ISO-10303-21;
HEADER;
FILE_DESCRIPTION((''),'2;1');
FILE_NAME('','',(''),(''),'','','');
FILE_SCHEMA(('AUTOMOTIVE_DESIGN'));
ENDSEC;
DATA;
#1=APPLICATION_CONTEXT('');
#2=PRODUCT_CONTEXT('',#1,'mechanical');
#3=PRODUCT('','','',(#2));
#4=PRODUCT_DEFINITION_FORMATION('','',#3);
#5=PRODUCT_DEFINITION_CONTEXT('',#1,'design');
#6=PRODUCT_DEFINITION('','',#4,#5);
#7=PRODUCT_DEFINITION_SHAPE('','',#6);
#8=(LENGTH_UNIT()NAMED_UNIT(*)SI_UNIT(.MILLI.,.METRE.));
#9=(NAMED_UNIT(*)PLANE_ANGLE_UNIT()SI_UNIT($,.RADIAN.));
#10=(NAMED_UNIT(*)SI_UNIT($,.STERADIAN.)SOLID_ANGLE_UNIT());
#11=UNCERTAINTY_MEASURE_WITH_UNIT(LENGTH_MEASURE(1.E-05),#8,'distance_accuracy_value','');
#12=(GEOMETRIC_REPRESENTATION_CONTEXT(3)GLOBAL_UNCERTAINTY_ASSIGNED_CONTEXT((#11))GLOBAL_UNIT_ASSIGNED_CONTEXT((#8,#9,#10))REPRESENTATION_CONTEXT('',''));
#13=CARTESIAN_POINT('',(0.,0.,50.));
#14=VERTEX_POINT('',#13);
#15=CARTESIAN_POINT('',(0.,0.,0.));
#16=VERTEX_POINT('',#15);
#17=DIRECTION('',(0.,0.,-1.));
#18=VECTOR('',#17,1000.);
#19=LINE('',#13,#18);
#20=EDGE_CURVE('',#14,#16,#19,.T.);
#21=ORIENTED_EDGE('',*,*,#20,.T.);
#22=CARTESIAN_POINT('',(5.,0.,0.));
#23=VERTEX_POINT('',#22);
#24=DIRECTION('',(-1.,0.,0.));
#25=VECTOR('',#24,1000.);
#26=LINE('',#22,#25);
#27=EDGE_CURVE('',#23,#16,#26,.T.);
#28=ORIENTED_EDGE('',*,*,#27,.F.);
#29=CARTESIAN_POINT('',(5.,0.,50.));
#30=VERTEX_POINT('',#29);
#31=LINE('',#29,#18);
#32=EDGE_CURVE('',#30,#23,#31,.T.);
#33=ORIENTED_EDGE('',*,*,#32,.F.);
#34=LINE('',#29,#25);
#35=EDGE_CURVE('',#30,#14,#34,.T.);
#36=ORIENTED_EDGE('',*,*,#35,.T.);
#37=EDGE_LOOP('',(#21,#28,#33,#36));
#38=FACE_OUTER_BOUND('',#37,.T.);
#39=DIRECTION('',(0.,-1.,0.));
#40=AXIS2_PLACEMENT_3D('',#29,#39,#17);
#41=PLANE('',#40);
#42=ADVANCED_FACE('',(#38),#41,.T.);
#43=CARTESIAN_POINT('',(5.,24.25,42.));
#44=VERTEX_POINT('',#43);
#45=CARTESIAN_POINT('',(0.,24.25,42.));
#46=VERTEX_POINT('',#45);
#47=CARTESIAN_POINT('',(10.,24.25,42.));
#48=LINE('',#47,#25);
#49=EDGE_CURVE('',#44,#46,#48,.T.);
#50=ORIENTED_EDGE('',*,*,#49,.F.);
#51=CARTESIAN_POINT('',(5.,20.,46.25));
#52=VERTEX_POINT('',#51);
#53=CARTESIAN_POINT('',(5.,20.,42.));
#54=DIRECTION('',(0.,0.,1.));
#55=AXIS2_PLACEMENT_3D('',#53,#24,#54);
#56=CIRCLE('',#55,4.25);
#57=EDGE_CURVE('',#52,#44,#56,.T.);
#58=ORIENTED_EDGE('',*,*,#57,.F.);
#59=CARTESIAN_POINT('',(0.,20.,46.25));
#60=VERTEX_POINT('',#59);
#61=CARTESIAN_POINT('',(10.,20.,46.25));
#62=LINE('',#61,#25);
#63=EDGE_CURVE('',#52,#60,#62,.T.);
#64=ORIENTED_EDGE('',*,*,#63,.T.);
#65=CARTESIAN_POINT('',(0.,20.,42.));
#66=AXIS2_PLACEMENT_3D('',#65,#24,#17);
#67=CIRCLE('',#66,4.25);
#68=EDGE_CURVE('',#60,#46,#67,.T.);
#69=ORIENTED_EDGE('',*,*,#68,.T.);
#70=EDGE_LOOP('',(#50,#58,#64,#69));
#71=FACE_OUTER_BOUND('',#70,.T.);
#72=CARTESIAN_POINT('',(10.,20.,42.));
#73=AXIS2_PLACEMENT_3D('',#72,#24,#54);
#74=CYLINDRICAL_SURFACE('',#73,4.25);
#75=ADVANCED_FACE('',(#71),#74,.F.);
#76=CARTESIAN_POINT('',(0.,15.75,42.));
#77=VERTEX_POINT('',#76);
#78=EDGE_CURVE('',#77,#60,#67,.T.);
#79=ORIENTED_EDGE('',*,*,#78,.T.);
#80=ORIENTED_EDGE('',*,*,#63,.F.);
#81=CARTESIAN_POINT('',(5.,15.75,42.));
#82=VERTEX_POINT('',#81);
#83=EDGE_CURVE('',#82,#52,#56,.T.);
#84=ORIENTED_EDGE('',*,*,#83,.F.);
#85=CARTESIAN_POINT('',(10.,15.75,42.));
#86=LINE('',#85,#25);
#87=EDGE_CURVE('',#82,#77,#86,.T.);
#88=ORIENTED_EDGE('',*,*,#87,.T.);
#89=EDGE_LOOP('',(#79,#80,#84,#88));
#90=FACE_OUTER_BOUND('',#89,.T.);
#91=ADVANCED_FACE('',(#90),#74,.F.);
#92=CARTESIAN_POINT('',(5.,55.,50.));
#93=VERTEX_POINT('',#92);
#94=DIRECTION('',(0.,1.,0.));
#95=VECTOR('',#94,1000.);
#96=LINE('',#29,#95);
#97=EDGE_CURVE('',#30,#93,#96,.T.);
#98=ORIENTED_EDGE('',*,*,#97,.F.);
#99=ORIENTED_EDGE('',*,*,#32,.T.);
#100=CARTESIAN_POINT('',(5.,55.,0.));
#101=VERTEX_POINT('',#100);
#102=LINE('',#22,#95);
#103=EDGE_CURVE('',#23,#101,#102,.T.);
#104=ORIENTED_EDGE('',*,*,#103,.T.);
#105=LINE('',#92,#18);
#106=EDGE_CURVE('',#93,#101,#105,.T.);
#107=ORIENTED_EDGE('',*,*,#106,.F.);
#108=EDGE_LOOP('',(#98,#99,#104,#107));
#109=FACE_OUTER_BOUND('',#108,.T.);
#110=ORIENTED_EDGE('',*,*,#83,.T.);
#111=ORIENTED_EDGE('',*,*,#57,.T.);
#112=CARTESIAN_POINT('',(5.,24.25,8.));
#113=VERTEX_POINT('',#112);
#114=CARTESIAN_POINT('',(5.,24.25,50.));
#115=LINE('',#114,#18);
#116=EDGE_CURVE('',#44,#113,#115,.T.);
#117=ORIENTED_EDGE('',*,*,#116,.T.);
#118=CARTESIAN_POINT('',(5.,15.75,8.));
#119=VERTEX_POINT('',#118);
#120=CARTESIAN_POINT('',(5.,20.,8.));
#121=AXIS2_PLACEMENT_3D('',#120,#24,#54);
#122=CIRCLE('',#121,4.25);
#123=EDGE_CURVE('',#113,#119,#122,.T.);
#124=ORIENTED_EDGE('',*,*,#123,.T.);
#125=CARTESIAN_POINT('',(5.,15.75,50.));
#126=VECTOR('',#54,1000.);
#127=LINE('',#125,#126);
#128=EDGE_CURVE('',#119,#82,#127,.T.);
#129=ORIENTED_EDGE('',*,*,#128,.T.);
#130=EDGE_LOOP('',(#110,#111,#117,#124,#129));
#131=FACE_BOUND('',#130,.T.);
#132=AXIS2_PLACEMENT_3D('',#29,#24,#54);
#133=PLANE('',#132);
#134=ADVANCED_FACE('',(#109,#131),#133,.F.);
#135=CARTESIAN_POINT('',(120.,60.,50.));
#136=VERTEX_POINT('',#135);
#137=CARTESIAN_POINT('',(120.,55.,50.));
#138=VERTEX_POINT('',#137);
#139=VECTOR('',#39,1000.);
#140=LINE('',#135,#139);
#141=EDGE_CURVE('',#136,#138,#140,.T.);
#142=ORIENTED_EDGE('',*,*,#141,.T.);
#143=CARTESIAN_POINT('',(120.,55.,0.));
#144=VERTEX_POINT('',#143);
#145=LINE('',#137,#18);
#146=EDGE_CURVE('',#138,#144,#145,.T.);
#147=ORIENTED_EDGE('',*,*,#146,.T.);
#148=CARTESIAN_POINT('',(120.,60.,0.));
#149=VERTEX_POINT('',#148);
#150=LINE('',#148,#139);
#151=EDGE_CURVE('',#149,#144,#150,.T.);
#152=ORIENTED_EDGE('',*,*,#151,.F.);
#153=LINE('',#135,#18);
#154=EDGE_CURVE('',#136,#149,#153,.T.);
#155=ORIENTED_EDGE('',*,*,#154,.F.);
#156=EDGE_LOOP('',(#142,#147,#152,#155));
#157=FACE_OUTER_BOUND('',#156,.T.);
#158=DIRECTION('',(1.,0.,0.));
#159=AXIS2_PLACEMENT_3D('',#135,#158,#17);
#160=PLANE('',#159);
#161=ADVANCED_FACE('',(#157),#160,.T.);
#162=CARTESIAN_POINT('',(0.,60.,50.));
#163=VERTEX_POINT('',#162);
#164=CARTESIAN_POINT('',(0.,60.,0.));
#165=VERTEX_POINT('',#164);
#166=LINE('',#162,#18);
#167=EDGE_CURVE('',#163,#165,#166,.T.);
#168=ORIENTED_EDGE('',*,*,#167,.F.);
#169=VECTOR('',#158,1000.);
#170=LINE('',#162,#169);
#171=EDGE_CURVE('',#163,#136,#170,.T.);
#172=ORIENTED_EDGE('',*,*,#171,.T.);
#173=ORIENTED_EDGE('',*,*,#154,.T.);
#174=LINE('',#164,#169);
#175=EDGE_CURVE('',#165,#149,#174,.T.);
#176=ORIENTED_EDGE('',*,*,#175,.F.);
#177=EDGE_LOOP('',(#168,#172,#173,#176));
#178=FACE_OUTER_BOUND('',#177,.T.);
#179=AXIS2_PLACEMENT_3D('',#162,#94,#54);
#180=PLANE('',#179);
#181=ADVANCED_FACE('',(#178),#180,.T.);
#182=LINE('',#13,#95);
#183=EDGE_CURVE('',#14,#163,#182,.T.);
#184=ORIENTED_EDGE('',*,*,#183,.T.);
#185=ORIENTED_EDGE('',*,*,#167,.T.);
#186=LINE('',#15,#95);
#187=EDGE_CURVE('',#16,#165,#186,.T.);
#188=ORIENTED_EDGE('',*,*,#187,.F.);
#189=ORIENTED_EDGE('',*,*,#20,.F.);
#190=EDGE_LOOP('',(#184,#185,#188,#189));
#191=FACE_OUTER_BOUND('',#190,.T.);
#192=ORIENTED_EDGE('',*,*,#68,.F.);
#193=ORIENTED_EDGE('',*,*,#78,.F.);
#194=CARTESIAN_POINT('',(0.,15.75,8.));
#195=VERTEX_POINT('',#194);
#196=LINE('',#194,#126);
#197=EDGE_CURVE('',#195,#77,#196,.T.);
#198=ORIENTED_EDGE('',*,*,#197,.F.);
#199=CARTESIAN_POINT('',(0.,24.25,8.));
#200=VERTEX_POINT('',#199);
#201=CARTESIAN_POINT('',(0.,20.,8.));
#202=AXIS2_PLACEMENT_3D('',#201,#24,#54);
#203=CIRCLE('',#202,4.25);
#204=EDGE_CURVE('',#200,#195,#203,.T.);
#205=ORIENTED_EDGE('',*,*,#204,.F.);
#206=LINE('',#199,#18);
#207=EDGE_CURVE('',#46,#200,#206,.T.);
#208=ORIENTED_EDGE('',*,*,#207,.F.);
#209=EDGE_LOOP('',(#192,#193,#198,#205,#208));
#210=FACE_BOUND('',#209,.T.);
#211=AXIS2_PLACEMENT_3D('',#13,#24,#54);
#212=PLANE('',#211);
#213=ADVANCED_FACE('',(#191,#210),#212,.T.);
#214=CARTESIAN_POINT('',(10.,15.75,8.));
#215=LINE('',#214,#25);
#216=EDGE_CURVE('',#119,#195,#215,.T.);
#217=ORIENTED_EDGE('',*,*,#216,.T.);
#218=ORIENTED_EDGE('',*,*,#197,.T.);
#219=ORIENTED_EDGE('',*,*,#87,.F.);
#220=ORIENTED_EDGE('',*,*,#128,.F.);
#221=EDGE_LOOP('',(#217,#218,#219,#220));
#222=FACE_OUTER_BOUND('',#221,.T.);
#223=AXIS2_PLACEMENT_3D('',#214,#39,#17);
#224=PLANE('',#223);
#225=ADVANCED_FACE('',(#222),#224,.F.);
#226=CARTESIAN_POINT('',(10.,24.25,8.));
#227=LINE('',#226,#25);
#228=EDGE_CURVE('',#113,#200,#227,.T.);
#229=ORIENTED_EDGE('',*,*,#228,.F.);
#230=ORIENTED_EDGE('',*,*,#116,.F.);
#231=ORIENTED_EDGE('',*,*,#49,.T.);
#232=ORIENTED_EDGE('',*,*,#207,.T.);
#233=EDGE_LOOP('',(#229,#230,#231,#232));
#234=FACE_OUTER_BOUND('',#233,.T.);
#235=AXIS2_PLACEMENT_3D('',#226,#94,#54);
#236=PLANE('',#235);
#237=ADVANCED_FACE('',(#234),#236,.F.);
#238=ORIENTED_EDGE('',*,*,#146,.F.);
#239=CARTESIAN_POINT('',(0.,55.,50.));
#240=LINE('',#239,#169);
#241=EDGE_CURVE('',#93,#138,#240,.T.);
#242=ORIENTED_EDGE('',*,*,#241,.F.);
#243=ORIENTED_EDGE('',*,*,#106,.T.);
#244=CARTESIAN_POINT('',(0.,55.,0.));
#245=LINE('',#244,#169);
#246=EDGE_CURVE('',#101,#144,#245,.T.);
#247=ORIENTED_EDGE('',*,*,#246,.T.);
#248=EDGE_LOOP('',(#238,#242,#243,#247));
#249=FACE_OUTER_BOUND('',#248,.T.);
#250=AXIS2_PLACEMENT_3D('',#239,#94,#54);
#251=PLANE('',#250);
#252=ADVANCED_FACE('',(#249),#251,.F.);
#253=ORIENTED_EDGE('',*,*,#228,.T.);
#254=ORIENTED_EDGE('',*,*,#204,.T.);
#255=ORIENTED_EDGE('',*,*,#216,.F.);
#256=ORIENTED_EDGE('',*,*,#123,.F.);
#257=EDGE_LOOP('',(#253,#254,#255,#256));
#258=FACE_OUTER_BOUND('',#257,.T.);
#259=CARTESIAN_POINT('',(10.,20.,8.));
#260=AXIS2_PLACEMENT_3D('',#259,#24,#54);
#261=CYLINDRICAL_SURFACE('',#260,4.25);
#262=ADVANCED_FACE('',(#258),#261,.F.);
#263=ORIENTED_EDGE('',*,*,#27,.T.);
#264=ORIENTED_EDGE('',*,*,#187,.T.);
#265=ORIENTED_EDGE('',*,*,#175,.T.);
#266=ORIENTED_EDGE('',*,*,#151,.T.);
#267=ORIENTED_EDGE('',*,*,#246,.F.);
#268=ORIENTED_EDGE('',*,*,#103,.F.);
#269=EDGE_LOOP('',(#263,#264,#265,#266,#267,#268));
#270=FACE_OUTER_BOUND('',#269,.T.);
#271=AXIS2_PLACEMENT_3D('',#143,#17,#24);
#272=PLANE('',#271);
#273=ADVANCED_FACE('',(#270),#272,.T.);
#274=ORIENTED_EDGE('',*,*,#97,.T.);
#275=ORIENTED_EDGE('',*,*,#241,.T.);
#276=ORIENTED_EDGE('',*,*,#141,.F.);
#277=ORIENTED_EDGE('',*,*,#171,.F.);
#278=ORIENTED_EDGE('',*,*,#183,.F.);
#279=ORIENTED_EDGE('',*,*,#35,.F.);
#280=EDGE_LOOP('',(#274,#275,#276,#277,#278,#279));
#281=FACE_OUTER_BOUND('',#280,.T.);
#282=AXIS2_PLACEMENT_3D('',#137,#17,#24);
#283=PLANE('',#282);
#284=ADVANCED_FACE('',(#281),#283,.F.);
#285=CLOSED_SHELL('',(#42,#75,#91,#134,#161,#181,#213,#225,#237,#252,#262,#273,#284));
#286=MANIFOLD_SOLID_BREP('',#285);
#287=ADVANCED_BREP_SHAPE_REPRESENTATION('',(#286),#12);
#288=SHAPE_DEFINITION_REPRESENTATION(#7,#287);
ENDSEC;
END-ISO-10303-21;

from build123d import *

# Parameters (mm, degrees)
EXTRUDE_1_DEPTH     = 50
CUT_EXTRUDE_1_DEPTH = 10


with BuildPart() as part:
    # 草图1 → 拉伸-薄壁1 (new body)
    with BuildSketch(Plane.XY):
        Polygon((0, 0), (0, 60), (120, 60), (120, 55), (5, 55), (5, 0), align=None)
    extrude(amount=EXTRUDE_1_DEPTH)

    # 草图2 → 切除-拉伸1 (cut)
    with BuildSketch(Plane.ZY):
        with BuildLine():
            Line((8, 24.25), (42, 24.25))
            ThreePointArc((42, 24.25), (46.25, 20), (42, 15.75))
            Line((42, 15.75), (8, 15.75))
            ThreePointArc((8, 15.75), (3.75, 20), (8, 24.25))
        make_face()
    extrude(amount=-CUT_EXTRUDE_1_DEPTH, mode=Mode.SUBTRACT)


solid = part.part
